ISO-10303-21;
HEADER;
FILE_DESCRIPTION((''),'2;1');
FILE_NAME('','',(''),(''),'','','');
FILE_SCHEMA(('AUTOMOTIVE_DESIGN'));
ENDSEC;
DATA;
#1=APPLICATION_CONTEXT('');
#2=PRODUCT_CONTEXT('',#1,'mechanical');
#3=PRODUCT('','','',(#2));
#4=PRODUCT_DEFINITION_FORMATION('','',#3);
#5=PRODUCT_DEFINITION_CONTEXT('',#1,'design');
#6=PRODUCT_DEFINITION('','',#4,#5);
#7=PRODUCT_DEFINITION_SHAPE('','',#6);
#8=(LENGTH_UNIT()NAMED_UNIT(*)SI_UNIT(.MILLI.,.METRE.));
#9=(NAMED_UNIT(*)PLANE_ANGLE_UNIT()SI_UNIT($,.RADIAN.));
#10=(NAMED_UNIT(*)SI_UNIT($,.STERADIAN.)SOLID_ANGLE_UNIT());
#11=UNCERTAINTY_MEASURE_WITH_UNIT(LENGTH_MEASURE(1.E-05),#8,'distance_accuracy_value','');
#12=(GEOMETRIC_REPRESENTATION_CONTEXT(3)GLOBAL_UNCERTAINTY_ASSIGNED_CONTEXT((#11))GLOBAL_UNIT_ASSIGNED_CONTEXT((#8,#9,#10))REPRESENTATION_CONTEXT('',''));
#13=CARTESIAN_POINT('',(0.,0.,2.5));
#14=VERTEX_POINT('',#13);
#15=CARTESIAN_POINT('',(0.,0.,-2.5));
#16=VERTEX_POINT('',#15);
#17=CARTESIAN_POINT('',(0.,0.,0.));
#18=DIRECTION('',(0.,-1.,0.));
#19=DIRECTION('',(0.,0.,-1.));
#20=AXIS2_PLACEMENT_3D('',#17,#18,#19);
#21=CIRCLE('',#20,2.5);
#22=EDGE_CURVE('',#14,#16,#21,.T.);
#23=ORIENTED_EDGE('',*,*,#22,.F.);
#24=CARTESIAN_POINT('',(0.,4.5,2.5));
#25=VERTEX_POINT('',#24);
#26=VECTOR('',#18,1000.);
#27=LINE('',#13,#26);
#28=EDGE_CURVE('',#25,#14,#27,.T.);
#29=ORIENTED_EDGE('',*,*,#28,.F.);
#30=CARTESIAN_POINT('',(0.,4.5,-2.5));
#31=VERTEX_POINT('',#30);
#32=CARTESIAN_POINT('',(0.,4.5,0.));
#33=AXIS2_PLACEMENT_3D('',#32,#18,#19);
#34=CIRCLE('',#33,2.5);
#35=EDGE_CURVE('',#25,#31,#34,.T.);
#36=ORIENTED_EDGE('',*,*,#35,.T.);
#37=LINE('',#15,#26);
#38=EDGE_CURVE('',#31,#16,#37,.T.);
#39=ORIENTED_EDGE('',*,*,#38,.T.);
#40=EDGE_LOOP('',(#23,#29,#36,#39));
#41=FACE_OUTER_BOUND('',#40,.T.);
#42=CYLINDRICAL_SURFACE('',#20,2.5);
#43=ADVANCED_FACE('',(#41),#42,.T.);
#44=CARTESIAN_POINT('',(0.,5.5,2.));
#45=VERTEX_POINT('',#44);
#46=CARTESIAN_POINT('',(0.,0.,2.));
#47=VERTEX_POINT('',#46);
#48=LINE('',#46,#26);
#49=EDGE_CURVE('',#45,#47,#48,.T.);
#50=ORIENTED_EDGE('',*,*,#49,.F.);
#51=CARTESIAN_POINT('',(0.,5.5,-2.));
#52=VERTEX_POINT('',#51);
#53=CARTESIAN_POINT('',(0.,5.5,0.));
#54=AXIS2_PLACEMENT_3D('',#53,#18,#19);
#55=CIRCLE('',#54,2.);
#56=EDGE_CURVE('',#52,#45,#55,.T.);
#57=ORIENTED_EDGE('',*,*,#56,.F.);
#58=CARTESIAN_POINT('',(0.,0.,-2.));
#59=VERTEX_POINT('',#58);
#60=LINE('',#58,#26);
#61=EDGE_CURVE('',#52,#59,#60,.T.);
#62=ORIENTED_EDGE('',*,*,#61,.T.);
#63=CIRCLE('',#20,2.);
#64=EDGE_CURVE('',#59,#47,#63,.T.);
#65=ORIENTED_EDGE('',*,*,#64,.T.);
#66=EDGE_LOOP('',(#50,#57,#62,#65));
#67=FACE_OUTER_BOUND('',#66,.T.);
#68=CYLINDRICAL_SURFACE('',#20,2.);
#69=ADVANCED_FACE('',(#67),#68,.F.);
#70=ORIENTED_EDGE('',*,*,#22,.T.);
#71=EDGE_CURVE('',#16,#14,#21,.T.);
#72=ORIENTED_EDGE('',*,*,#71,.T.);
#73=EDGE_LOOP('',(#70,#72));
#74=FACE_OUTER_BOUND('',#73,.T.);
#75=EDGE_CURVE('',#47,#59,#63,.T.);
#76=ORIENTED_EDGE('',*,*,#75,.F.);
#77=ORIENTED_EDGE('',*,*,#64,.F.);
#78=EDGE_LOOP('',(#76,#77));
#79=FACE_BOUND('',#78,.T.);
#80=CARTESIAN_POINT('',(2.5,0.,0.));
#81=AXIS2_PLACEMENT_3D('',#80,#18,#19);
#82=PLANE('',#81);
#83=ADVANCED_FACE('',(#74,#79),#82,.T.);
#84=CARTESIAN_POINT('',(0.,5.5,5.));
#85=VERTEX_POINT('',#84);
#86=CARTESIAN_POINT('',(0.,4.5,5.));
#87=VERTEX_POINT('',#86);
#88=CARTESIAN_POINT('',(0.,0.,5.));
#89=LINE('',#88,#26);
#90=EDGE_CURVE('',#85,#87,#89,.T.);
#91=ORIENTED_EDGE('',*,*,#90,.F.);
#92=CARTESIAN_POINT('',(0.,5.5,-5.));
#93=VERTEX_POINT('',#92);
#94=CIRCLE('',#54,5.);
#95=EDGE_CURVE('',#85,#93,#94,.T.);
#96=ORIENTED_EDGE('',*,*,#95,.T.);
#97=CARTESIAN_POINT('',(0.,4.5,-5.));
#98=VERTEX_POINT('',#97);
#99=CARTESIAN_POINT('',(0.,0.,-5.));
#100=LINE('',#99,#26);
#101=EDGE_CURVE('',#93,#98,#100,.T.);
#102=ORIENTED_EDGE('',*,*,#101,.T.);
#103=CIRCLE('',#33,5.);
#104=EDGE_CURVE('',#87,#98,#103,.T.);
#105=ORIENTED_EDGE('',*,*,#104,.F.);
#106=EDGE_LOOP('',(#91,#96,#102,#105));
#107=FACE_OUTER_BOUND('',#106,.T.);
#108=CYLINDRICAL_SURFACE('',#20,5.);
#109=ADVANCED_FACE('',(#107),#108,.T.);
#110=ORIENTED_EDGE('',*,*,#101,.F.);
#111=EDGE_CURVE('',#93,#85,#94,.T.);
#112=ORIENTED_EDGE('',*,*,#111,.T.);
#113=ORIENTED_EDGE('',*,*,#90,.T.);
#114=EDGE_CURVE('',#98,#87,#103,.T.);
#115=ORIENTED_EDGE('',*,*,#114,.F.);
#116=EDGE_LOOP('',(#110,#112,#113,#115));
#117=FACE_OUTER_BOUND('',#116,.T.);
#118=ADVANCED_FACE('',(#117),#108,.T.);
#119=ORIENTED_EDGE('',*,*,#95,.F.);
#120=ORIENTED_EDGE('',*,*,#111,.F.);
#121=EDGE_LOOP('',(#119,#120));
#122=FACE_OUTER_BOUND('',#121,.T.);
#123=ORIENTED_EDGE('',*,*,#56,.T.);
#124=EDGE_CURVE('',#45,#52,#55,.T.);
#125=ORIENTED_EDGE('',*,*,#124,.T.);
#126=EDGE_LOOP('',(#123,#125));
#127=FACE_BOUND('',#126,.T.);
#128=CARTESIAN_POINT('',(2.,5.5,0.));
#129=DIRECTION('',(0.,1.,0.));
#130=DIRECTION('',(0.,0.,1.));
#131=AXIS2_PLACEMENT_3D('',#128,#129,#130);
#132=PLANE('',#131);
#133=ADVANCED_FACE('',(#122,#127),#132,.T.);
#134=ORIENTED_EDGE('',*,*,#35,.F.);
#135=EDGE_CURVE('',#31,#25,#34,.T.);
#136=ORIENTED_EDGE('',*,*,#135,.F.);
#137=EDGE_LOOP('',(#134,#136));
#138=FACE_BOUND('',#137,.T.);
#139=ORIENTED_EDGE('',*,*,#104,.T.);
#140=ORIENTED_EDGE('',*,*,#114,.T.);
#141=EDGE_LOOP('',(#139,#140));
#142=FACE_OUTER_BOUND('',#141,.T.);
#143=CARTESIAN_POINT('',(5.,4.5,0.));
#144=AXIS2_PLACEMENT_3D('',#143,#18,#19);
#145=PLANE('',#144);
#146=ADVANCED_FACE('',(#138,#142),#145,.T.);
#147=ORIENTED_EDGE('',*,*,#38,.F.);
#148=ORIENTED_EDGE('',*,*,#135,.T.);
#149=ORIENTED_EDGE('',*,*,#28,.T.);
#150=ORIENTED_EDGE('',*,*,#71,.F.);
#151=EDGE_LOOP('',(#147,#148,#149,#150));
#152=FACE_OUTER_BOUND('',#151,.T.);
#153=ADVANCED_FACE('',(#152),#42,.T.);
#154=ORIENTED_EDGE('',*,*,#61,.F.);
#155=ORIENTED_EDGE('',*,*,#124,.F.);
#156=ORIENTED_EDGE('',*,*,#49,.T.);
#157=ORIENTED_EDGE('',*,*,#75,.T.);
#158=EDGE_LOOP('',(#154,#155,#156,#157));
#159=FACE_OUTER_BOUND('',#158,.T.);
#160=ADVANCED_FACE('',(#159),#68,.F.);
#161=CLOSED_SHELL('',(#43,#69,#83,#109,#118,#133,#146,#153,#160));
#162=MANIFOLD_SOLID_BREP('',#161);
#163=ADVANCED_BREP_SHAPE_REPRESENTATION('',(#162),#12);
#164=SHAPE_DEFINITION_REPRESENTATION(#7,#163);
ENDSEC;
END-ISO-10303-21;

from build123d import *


with BuildPart() as part:
    # Sketch1 → Revolve1 (revolve)
    with BuildSketch(Plane.XY, mode=Mode.PRIVATE) as revolve1_sk:
        Polygon((2, 5.5), (5, 5.5), (5, 4.5), (2.5, 4.5), (2.5, 0), (2, 0), align=None)
    revolve(revolve1_sk.sketch.rotate(Axis((0, 0, 0), (0, 1, 0)), 90), axis=Axis((0, 0, 0), (0, 1, 0)))


solid = part.part
